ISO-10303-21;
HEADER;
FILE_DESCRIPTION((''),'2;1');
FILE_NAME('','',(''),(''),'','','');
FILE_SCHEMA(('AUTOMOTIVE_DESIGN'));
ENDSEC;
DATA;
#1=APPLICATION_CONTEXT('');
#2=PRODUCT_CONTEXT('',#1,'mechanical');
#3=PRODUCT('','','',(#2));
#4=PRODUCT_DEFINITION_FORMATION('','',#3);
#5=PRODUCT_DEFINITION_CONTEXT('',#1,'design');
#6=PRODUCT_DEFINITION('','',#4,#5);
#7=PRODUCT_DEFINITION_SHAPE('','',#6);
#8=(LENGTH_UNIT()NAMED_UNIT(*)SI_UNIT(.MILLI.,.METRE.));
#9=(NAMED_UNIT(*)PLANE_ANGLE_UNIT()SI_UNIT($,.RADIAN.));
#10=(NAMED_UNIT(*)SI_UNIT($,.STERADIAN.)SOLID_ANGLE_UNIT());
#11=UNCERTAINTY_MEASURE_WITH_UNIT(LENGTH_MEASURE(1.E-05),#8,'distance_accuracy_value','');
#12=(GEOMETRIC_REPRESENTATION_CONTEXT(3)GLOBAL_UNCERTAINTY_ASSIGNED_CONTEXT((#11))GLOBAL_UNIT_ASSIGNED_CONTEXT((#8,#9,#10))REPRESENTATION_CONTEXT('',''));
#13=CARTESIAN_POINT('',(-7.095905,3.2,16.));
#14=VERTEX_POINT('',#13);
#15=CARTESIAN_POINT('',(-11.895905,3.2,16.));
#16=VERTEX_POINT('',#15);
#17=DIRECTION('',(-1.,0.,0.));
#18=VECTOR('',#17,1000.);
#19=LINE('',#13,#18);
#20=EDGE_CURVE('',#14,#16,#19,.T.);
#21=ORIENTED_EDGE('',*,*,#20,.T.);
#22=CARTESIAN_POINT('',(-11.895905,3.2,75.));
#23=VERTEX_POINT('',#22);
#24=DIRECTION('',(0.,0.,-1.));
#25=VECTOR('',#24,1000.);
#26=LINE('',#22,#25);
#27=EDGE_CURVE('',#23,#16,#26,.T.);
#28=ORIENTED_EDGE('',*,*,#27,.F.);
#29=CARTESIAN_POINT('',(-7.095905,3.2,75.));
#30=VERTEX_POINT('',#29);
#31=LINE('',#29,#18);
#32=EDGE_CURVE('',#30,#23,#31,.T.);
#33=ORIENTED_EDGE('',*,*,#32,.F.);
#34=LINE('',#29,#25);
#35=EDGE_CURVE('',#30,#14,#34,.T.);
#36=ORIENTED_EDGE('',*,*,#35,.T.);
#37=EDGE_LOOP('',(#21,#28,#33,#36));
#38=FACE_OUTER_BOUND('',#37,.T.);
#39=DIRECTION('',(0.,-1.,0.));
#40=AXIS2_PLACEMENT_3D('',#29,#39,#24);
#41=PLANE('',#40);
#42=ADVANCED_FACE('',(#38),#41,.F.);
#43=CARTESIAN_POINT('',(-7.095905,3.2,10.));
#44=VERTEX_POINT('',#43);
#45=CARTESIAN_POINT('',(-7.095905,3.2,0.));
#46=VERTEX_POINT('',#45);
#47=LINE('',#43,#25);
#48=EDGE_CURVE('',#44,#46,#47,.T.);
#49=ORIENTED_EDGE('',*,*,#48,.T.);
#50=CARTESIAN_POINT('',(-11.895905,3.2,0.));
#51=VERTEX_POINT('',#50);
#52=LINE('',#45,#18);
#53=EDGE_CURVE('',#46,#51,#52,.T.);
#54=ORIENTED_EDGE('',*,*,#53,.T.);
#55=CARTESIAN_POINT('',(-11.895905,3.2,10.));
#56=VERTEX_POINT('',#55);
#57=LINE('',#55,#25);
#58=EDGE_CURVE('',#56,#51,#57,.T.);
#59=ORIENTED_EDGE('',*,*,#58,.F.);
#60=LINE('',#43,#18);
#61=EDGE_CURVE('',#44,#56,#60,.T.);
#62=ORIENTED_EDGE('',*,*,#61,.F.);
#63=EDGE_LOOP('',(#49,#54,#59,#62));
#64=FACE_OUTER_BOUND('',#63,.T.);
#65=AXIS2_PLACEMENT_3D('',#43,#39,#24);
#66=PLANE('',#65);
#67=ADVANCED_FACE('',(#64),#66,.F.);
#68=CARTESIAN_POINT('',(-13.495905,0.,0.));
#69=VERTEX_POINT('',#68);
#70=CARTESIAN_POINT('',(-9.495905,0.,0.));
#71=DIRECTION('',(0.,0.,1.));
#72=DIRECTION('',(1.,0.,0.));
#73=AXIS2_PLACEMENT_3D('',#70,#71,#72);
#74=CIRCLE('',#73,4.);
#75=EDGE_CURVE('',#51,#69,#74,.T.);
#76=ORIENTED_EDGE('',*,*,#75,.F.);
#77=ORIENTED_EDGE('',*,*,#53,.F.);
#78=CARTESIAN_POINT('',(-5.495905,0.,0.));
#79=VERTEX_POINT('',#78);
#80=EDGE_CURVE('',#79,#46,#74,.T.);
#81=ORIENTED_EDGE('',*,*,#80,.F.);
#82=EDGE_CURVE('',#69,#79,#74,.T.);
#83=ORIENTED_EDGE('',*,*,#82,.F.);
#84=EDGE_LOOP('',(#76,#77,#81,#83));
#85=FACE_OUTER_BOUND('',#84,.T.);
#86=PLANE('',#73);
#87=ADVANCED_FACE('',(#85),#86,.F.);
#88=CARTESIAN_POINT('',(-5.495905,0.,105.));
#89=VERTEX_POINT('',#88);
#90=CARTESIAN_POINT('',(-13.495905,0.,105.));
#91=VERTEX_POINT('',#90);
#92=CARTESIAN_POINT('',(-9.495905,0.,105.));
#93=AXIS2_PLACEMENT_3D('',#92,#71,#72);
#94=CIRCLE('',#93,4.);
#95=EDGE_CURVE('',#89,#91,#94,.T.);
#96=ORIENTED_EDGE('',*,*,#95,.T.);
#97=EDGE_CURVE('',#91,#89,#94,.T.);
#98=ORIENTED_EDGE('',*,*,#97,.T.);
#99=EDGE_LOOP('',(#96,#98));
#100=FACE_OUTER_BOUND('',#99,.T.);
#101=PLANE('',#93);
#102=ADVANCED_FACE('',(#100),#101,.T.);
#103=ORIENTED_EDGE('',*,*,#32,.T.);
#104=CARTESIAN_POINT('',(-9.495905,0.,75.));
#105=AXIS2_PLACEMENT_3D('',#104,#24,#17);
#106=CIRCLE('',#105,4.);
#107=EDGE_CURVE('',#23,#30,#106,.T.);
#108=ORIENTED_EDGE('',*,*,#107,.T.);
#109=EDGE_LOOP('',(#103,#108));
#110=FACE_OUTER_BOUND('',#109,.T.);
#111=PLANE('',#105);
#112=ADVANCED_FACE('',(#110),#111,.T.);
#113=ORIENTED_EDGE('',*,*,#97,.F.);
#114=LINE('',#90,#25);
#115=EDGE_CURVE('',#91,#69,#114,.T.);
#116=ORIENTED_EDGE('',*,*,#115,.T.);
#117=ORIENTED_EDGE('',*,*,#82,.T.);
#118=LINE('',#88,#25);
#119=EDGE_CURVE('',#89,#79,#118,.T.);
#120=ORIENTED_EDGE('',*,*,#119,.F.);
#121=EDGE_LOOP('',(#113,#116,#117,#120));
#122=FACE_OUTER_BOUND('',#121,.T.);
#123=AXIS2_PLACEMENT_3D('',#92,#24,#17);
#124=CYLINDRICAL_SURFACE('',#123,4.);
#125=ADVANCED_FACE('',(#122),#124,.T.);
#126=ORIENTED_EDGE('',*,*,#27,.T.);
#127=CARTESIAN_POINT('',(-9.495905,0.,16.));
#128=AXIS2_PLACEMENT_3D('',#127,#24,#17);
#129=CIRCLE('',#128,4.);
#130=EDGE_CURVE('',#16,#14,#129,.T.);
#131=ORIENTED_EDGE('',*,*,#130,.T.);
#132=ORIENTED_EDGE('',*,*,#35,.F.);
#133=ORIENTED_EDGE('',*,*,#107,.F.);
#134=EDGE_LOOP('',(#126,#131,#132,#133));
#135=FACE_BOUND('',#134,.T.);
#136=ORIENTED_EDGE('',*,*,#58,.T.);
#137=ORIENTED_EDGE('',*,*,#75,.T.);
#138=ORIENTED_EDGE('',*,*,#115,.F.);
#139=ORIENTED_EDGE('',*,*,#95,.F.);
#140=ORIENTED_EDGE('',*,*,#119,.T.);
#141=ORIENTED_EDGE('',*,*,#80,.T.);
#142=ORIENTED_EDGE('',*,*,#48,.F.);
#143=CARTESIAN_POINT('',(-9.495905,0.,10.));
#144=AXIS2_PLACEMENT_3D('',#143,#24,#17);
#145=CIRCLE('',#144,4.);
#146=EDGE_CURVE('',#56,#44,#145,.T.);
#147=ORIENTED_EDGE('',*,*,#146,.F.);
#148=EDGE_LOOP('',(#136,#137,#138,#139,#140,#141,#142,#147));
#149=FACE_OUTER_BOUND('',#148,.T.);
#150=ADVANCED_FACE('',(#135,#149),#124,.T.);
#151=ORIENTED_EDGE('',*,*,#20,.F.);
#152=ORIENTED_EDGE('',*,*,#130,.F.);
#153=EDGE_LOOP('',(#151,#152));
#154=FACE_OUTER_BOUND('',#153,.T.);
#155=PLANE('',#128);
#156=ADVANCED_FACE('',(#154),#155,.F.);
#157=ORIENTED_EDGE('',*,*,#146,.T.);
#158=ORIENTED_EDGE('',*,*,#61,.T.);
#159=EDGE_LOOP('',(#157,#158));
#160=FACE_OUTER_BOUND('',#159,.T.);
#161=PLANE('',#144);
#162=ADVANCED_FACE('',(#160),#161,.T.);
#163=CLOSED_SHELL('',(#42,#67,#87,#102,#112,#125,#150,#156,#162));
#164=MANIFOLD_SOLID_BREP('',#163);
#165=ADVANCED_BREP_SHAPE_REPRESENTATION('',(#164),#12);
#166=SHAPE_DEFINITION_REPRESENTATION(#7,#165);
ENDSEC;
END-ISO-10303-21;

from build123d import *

# Parameters (mm, degrees)
SKETCH_1_R          = 4
EXTRUDE_1_DEPTH     = 105
CUT_EXTRUDE_1_DEPTH = 10
CUT_EXTRUDE_2_DEPTH = 59


with BuildPart() as part:
    # 草图1 → 凸台-拉伸1 (new body)
    with BuildSketch(Plane.XY):
        with Locations((-9.495904584, 0)):
            Circle(SKETCH_1_R)
    extrude(amount=EXTRUDE_1_DEPTH)

    # 草图2 → 切除-拉伸1 (cut)
    with BuildSketch(Plane(origin=(0, 0, 0), x_dir=(-1, 0, 0), z_dir=(0, 0, -1))):
        with BuildLine():
            Line((7.095904584, 3.2), (11.895904584, 3.2))
            ThreePointArc((11.895904584, 3.2), (9.495904584, 4), (7.095904584, 3.2))
        make_face()
    extrude(amount=-CUT_EXTRUDE_1_DEPTH, mode=Mode.SUBTRACT)

    # 草图3 → 切除-拉伸2 (cut)
    with BuildSketch(Plane(origin=(0, 0, 16), x_dir=(-1, 0, 0), z_dir=(0, 0, -1))):
        with BuildLine():
            Line((7.095904584, 3.2), (11.895904584, 3.2))
            ThreePointArc((11.895904584, 3.2), (9.495904584, 4), (7.095904584, 3.2))
        make_face()
    extrude(amount=-CUT_EXTRUDE_2_DEPTH, mode=Mode.SUBTRACT)


solid = part.part
